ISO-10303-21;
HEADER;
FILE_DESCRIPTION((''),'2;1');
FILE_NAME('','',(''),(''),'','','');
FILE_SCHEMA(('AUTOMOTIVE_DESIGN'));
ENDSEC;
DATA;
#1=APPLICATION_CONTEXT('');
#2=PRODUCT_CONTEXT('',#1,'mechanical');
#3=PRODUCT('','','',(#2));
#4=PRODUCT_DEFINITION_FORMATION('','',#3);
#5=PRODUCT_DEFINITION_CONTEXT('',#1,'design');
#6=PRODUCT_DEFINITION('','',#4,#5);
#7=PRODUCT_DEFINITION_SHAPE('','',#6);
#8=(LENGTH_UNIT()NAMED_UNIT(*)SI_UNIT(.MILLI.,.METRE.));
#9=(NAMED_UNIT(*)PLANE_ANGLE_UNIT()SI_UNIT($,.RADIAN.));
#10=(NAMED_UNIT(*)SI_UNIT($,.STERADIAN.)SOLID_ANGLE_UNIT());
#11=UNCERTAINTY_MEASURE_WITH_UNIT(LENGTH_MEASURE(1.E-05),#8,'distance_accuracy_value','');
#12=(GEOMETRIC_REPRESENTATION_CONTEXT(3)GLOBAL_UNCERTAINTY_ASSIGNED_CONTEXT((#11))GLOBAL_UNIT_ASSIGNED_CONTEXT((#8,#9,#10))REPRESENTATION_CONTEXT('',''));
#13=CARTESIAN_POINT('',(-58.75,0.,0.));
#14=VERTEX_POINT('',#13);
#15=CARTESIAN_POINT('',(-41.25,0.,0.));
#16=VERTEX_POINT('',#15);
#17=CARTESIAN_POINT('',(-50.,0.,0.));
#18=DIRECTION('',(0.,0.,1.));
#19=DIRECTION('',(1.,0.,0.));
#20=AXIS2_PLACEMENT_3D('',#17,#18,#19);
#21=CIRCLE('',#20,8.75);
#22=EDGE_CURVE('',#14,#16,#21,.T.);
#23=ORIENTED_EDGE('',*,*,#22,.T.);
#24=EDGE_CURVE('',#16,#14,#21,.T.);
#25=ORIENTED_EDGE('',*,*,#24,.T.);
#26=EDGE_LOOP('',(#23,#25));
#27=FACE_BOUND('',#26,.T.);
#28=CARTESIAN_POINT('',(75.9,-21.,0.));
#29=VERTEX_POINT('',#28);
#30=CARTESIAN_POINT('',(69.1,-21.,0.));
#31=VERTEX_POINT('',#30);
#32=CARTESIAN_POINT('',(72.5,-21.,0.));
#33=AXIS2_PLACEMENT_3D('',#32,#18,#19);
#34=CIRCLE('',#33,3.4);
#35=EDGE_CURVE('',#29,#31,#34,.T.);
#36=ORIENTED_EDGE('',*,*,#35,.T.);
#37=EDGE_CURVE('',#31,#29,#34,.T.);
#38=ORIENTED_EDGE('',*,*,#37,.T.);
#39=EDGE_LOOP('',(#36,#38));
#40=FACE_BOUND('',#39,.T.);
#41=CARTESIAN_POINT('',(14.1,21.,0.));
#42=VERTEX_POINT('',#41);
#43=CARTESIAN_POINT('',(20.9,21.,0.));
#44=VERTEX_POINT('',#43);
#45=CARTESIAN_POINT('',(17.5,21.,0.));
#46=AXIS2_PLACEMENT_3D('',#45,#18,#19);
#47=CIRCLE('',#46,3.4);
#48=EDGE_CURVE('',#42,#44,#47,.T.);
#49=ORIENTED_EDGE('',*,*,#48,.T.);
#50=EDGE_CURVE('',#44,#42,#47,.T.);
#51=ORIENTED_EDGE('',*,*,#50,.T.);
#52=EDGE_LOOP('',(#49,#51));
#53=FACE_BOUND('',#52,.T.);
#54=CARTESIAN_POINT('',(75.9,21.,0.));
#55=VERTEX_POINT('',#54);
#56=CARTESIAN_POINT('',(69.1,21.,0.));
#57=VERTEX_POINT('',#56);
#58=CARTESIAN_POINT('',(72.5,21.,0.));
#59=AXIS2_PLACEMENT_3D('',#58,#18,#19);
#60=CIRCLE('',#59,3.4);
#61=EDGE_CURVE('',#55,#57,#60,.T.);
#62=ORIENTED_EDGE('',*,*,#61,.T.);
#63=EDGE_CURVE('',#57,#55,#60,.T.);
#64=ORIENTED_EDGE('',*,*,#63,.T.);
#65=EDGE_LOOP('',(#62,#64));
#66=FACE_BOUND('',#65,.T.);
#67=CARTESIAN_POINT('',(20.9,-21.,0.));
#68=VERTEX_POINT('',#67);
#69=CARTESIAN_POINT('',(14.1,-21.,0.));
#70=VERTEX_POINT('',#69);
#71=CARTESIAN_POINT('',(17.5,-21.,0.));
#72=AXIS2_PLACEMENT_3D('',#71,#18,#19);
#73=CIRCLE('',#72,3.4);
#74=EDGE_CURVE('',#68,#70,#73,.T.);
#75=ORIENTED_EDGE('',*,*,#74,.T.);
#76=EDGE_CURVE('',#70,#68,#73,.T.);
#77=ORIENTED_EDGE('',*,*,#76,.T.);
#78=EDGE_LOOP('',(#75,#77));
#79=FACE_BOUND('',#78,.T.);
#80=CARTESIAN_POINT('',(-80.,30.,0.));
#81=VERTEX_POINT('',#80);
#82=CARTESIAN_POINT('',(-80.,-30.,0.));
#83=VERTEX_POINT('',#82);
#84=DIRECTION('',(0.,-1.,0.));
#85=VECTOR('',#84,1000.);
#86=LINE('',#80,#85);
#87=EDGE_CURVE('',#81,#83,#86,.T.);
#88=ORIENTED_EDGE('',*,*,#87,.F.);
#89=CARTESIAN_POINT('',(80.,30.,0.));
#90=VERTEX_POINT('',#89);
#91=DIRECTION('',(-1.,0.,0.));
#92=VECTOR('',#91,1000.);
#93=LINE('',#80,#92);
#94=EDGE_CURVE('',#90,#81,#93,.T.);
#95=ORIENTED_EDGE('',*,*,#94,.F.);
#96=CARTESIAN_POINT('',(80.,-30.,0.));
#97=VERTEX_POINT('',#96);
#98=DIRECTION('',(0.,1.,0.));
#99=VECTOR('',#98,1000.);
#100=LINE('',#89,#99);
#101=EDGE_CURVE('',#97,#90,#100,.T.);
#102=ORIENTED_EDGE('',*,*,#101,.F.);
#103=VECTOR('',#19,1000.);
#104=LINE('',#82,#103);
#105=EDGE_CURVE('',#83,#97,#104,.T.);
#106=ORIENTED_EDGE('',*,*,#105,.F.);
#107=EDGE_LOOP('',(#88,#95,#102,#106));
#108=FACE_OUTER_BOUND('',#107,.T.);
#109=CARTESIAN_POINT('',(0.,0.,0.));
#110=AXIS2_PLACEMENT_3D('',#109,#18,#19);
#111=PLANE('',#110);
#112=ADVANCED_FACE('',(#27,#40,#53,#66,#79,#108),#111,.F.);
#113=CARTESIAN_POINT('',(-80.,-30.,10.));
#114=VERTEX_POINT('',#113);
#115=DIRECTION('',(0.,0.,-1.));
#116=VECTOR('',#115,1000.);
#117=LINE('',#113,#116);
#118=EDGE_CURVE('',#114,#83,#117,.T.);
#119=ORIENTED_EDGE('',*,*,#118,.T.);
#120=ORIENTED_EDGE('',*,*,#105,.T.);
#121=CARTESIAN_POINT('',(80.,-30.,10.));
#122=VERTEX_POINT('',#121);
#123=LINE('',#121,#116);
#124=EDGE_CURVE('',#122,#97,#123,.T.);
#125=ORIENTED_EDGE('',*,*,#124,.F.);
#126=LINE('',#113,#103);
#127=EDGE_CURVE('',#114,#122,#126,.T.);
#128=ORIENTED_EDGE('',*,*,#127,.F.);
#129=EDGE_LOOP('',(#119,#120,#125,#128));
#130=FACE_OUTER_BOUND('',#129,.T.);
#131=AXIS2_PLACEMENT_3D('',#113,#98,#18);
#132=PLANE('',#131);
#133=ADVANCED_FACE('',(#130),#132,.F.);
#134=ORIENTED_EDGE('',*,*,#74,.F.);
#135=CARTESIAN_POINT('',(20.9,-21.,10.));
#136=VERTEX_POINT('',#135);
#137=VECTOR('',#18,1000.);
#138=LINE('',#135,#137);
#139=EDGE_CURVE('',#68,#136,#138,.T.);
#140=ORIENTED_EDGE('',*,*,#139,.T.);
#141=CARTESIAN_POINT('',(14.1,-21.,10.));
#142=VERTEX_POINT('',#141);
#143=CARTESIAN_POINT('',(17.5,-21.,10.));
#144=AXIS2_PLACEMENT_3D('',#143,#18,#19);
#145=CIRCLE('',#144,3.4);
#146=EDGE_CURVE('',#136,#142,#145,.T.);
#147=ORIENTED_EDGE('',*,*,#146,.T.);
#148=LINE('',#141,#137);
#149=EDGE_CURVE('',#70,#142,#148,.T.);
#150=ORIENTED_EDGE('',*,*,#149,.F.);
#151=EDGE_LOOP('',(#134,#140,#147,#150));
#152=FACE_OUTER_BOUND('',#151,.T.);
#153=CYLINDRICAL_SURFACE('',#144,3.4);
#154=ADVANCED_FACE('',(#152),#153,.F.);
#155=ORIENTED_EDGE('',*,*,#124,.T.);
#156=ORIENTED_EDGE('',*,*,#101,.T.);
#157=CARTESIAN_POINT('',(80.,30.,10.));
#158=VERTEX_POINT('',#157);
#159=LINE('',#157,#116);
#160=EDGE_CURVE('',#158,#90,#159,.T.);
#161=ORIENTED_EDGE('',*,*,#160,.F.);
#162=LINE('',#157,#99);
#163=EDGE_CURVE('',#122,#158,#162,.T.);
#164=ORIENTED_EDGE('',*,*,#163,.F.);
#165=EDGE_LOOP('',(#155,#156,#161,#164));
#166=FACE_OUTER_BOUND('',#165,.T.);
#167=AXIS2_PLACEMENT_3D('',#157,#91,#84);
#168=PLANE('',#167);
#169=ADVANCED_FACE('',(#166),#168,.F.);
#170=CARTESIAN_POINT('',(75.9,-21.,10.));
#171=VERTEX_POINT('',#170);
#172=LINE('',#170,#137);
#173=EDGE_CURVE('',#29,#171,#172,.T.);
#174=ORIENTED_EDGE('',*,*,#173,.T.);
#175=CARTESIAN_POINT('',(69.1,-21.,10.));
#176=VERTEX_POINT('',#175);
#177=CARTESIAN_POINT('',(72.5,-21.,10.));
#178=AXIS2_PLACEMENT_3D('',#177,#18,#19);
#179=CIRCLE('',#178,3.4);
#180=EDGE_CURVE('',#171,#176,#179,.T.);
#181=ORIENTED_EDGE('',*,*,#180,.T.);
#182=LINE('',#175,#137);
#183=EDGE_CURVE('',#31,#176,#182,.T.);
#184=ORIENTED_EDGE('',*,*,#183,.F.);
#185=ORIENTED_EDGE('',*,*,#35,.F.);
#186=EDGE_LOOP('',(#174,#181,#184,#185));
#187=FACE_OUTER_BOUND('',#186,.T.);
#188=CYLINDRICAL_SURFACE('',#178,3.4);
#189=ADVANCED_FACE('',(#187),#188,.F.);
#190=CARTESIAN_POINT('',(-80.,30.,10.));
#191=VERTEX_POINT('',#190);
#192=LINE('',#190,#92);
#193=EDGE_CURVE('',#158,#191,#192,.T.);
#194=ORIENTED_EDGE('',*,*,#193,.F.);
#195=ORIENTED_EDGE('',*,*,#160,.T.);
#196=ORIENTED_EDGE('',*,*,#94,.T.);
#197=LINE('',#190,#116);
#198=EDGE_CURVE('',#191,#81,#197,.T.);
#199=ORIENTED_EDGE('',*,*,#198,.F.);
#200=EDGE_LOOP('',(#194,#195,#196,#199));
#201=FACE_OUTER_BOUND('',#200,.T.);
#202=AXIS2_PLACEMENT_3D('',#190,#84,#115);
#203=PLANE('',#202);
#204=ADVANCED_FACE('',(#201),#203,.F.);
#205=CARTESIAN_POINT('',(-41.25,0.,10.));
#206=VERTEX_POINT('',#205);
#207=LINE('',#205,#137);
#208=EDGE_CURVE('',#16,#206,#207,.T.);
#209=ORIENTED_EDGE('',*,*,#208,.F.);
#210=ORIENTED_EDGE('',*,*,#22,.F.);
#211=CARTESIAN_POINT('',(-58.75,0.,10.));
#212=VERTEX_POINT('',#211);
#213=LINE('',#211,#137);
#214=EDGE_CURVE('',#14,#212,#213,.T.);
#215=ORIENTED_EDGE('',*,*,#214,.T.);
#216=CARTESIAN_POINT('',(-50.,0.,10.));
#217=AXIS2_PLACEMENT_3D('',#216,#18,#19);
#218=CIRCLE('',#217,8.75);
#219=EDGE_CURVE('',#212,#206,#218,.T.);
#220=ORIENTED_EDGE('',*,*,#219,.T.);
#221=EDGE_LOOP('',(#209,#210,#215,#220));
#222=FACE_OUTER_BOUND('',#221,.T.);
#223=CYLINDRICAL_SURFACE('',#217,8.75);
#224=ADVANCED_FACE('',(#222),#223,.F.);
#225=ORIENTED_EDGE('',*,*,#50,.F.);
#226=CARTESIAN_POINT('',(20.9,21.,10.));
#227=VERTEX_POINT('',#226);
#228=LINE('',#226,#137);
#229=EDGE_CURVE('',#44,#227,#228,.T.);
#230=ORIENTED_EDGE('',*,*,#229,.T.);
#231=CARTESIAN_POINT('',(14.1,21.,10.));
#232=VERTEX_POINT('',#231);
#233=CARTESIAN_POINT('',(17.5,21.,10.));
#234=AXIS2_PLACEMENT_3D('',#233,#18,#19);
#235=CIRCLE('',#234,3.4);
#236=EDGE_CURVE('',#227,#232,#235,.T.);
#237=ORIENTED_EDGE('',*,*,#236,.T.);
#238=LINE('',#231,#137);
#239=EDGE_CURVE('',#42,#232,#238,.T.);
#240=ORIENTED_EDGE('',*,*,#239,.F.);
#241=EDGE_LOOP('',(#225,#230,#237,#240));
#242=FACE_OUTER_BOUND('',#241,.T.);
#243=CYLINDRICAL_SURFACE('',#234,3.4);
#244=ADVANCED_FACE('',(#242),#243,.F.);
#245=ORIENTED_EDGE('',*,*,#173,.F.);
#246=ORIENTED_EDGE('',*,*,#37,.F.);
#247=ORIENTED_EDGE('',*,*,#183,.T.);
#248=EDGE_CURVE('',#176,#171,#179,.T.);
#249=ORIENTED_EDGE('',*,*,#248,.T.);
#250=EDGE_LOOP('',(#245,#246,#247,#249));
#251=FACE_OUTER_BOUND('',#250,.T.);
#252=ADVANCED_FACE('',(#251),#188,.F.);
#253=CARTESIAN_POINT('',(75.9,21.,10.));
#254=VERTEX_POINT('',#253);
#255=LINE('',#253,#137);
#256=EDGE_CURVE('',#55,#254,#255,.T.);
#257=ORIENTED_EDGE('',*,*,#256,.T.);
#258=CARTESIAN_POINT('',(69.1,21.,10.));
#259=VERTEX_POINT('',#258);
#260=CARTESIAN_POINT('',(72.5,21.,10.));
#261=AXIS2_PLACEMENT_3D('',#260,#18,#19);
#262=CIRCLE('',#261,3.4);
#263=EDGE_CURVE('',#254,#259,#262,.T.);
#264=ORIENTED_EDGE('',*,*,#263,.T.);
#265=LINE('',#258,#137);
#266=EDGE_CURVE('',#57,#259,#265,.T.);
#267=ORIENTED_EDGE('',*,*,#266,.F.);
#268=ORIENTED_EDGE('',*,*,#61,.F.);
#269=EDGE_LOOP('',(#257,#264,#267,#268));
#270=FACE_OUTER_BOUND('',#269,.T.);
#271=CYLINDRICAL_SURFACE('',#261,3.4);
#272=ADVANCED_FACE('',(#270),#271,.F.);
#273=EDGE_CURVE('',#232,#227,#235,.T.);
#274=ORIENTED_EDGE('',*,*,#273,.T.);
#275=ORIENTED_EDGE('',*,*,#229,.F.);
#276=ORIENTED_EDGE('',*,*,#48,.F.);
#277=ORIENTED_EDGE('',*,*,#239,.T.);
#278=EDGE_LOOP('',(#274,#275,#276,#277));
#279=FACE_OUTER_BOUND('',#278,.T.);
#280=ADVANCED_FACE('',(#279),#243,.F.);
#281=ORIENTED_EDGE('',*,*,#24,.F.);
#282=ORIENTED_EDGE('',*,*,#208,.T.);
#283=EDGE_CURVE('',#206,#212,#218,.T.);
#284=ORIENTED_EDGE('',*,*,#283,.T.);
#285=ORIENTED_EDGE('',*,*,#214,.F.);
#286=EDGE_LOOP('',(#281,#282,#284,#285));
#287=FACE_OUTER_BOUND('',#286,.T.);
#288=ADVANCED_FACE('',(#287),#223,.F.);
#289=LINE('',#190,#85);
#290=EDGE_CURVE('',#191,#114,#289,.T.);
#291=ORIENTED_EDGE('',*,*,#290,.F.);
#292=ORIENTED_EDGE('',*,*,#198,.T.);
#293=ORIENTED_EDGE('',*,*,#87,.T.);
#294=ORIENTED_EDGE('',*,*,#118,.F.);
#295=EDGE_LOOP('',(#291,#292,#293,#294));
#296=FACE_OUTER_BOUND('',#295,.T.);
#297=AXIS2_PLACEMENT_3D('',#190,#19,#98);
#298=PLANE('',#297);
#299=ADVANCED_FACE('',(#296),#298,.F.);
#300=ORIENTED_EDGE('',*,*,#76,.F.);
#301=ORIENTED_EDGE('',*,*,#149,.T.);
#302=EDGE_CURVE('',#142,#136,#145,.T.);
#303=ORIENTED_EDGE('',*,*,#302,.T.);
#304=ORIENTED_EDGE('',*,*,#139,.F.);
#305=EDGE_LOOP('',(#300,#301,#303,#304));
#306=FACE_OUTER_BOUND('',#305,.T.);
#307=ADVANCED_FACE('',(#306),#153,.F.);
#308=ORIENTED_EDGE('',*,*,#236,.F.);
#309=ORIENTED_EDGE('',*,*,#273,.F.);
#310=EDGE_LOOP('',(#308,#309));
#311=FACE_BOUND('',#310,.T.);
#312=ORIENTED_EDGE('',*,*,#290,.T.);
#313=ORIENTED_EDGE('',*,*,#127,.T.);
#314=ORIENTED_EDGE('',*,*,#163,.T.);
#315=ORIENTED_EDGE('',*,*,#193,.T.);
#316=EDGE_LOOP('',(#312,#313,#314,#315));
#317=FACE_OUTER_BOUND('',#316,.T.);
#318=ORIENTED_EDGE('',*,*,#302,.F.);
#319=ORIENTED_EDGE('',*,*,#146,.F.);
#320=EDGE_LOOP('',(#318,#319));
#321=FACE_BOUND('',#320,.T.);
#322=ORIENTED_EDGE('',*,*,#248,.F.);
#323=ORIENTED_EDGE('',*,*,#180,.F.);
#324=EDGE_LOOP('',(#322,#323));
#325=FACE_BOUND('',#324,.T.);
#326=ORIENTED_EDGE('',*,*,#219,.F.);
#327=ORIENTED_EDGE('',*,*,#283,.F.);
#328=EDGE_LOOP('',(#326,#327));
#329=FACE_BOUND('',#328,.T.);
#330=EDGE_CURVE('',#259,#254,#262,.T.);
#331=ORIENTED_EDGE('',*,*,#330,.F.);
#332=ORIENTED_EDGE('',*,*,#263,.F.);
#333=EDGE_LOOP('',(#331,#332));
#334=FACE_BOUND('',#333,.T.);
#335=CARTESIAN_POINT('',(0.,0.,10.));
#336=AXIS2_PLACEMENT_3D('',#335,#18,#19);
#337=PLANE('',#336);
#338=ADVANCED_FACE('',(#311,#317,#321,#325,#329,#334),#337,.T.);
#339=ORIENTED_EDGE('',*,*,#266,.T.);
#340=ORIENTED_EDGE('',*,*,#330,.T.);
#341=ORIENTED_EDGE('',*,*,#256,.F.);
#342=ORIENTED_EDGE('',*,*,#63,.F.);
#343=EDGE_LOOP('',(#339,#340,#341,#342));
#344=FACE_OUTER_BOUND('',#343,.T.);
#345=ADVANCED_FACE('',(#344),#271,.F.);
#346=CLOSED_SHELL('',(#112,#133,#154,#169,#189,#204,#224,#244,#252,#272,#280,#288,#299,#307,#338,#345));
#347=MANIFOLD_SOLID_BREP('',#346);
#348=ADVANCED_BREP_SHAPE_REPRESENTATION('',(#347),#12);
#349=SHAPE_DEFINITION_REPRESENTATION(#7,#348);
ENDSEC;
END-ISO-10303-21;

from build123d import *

# Parameters (mm, degrees)
SKETCH_1_W          = 160
SKETCH_1_H          = 60
EXTRUDE_1_DEPTH     = 10
HOLE_WIZARD_M20_1_D = 17.5
HOLE_WIZARD_M8_1_D  = 6.8


with BuildPart() as part:
    # 草图1 → 凸台-拉伸1 (new body)
    with BuildSketch(Plane.XY):
        Rectangle(SKETCH_1_W, SKETCH_1_H)
    extrude(amount=EXTRUDE_1_DEPTH)

    # M20 螺纹孔1 (through all)
    with Locations(Plane.XY.offset(10)):
        with Locations((-50, 0)):
            Hole(HOLE_WIZARD_M20_1_D / 2)

    # M8 螺纹孔1 (through all)
    with Locations(Plane.XY.offset(10)):
        with Locations((17.5, 21), (72.5, 21), (17.5, -21), (72.5, -21)):
            Hole(HOLE_WIZARD_M8_1_D / 2)


solid = part.part
